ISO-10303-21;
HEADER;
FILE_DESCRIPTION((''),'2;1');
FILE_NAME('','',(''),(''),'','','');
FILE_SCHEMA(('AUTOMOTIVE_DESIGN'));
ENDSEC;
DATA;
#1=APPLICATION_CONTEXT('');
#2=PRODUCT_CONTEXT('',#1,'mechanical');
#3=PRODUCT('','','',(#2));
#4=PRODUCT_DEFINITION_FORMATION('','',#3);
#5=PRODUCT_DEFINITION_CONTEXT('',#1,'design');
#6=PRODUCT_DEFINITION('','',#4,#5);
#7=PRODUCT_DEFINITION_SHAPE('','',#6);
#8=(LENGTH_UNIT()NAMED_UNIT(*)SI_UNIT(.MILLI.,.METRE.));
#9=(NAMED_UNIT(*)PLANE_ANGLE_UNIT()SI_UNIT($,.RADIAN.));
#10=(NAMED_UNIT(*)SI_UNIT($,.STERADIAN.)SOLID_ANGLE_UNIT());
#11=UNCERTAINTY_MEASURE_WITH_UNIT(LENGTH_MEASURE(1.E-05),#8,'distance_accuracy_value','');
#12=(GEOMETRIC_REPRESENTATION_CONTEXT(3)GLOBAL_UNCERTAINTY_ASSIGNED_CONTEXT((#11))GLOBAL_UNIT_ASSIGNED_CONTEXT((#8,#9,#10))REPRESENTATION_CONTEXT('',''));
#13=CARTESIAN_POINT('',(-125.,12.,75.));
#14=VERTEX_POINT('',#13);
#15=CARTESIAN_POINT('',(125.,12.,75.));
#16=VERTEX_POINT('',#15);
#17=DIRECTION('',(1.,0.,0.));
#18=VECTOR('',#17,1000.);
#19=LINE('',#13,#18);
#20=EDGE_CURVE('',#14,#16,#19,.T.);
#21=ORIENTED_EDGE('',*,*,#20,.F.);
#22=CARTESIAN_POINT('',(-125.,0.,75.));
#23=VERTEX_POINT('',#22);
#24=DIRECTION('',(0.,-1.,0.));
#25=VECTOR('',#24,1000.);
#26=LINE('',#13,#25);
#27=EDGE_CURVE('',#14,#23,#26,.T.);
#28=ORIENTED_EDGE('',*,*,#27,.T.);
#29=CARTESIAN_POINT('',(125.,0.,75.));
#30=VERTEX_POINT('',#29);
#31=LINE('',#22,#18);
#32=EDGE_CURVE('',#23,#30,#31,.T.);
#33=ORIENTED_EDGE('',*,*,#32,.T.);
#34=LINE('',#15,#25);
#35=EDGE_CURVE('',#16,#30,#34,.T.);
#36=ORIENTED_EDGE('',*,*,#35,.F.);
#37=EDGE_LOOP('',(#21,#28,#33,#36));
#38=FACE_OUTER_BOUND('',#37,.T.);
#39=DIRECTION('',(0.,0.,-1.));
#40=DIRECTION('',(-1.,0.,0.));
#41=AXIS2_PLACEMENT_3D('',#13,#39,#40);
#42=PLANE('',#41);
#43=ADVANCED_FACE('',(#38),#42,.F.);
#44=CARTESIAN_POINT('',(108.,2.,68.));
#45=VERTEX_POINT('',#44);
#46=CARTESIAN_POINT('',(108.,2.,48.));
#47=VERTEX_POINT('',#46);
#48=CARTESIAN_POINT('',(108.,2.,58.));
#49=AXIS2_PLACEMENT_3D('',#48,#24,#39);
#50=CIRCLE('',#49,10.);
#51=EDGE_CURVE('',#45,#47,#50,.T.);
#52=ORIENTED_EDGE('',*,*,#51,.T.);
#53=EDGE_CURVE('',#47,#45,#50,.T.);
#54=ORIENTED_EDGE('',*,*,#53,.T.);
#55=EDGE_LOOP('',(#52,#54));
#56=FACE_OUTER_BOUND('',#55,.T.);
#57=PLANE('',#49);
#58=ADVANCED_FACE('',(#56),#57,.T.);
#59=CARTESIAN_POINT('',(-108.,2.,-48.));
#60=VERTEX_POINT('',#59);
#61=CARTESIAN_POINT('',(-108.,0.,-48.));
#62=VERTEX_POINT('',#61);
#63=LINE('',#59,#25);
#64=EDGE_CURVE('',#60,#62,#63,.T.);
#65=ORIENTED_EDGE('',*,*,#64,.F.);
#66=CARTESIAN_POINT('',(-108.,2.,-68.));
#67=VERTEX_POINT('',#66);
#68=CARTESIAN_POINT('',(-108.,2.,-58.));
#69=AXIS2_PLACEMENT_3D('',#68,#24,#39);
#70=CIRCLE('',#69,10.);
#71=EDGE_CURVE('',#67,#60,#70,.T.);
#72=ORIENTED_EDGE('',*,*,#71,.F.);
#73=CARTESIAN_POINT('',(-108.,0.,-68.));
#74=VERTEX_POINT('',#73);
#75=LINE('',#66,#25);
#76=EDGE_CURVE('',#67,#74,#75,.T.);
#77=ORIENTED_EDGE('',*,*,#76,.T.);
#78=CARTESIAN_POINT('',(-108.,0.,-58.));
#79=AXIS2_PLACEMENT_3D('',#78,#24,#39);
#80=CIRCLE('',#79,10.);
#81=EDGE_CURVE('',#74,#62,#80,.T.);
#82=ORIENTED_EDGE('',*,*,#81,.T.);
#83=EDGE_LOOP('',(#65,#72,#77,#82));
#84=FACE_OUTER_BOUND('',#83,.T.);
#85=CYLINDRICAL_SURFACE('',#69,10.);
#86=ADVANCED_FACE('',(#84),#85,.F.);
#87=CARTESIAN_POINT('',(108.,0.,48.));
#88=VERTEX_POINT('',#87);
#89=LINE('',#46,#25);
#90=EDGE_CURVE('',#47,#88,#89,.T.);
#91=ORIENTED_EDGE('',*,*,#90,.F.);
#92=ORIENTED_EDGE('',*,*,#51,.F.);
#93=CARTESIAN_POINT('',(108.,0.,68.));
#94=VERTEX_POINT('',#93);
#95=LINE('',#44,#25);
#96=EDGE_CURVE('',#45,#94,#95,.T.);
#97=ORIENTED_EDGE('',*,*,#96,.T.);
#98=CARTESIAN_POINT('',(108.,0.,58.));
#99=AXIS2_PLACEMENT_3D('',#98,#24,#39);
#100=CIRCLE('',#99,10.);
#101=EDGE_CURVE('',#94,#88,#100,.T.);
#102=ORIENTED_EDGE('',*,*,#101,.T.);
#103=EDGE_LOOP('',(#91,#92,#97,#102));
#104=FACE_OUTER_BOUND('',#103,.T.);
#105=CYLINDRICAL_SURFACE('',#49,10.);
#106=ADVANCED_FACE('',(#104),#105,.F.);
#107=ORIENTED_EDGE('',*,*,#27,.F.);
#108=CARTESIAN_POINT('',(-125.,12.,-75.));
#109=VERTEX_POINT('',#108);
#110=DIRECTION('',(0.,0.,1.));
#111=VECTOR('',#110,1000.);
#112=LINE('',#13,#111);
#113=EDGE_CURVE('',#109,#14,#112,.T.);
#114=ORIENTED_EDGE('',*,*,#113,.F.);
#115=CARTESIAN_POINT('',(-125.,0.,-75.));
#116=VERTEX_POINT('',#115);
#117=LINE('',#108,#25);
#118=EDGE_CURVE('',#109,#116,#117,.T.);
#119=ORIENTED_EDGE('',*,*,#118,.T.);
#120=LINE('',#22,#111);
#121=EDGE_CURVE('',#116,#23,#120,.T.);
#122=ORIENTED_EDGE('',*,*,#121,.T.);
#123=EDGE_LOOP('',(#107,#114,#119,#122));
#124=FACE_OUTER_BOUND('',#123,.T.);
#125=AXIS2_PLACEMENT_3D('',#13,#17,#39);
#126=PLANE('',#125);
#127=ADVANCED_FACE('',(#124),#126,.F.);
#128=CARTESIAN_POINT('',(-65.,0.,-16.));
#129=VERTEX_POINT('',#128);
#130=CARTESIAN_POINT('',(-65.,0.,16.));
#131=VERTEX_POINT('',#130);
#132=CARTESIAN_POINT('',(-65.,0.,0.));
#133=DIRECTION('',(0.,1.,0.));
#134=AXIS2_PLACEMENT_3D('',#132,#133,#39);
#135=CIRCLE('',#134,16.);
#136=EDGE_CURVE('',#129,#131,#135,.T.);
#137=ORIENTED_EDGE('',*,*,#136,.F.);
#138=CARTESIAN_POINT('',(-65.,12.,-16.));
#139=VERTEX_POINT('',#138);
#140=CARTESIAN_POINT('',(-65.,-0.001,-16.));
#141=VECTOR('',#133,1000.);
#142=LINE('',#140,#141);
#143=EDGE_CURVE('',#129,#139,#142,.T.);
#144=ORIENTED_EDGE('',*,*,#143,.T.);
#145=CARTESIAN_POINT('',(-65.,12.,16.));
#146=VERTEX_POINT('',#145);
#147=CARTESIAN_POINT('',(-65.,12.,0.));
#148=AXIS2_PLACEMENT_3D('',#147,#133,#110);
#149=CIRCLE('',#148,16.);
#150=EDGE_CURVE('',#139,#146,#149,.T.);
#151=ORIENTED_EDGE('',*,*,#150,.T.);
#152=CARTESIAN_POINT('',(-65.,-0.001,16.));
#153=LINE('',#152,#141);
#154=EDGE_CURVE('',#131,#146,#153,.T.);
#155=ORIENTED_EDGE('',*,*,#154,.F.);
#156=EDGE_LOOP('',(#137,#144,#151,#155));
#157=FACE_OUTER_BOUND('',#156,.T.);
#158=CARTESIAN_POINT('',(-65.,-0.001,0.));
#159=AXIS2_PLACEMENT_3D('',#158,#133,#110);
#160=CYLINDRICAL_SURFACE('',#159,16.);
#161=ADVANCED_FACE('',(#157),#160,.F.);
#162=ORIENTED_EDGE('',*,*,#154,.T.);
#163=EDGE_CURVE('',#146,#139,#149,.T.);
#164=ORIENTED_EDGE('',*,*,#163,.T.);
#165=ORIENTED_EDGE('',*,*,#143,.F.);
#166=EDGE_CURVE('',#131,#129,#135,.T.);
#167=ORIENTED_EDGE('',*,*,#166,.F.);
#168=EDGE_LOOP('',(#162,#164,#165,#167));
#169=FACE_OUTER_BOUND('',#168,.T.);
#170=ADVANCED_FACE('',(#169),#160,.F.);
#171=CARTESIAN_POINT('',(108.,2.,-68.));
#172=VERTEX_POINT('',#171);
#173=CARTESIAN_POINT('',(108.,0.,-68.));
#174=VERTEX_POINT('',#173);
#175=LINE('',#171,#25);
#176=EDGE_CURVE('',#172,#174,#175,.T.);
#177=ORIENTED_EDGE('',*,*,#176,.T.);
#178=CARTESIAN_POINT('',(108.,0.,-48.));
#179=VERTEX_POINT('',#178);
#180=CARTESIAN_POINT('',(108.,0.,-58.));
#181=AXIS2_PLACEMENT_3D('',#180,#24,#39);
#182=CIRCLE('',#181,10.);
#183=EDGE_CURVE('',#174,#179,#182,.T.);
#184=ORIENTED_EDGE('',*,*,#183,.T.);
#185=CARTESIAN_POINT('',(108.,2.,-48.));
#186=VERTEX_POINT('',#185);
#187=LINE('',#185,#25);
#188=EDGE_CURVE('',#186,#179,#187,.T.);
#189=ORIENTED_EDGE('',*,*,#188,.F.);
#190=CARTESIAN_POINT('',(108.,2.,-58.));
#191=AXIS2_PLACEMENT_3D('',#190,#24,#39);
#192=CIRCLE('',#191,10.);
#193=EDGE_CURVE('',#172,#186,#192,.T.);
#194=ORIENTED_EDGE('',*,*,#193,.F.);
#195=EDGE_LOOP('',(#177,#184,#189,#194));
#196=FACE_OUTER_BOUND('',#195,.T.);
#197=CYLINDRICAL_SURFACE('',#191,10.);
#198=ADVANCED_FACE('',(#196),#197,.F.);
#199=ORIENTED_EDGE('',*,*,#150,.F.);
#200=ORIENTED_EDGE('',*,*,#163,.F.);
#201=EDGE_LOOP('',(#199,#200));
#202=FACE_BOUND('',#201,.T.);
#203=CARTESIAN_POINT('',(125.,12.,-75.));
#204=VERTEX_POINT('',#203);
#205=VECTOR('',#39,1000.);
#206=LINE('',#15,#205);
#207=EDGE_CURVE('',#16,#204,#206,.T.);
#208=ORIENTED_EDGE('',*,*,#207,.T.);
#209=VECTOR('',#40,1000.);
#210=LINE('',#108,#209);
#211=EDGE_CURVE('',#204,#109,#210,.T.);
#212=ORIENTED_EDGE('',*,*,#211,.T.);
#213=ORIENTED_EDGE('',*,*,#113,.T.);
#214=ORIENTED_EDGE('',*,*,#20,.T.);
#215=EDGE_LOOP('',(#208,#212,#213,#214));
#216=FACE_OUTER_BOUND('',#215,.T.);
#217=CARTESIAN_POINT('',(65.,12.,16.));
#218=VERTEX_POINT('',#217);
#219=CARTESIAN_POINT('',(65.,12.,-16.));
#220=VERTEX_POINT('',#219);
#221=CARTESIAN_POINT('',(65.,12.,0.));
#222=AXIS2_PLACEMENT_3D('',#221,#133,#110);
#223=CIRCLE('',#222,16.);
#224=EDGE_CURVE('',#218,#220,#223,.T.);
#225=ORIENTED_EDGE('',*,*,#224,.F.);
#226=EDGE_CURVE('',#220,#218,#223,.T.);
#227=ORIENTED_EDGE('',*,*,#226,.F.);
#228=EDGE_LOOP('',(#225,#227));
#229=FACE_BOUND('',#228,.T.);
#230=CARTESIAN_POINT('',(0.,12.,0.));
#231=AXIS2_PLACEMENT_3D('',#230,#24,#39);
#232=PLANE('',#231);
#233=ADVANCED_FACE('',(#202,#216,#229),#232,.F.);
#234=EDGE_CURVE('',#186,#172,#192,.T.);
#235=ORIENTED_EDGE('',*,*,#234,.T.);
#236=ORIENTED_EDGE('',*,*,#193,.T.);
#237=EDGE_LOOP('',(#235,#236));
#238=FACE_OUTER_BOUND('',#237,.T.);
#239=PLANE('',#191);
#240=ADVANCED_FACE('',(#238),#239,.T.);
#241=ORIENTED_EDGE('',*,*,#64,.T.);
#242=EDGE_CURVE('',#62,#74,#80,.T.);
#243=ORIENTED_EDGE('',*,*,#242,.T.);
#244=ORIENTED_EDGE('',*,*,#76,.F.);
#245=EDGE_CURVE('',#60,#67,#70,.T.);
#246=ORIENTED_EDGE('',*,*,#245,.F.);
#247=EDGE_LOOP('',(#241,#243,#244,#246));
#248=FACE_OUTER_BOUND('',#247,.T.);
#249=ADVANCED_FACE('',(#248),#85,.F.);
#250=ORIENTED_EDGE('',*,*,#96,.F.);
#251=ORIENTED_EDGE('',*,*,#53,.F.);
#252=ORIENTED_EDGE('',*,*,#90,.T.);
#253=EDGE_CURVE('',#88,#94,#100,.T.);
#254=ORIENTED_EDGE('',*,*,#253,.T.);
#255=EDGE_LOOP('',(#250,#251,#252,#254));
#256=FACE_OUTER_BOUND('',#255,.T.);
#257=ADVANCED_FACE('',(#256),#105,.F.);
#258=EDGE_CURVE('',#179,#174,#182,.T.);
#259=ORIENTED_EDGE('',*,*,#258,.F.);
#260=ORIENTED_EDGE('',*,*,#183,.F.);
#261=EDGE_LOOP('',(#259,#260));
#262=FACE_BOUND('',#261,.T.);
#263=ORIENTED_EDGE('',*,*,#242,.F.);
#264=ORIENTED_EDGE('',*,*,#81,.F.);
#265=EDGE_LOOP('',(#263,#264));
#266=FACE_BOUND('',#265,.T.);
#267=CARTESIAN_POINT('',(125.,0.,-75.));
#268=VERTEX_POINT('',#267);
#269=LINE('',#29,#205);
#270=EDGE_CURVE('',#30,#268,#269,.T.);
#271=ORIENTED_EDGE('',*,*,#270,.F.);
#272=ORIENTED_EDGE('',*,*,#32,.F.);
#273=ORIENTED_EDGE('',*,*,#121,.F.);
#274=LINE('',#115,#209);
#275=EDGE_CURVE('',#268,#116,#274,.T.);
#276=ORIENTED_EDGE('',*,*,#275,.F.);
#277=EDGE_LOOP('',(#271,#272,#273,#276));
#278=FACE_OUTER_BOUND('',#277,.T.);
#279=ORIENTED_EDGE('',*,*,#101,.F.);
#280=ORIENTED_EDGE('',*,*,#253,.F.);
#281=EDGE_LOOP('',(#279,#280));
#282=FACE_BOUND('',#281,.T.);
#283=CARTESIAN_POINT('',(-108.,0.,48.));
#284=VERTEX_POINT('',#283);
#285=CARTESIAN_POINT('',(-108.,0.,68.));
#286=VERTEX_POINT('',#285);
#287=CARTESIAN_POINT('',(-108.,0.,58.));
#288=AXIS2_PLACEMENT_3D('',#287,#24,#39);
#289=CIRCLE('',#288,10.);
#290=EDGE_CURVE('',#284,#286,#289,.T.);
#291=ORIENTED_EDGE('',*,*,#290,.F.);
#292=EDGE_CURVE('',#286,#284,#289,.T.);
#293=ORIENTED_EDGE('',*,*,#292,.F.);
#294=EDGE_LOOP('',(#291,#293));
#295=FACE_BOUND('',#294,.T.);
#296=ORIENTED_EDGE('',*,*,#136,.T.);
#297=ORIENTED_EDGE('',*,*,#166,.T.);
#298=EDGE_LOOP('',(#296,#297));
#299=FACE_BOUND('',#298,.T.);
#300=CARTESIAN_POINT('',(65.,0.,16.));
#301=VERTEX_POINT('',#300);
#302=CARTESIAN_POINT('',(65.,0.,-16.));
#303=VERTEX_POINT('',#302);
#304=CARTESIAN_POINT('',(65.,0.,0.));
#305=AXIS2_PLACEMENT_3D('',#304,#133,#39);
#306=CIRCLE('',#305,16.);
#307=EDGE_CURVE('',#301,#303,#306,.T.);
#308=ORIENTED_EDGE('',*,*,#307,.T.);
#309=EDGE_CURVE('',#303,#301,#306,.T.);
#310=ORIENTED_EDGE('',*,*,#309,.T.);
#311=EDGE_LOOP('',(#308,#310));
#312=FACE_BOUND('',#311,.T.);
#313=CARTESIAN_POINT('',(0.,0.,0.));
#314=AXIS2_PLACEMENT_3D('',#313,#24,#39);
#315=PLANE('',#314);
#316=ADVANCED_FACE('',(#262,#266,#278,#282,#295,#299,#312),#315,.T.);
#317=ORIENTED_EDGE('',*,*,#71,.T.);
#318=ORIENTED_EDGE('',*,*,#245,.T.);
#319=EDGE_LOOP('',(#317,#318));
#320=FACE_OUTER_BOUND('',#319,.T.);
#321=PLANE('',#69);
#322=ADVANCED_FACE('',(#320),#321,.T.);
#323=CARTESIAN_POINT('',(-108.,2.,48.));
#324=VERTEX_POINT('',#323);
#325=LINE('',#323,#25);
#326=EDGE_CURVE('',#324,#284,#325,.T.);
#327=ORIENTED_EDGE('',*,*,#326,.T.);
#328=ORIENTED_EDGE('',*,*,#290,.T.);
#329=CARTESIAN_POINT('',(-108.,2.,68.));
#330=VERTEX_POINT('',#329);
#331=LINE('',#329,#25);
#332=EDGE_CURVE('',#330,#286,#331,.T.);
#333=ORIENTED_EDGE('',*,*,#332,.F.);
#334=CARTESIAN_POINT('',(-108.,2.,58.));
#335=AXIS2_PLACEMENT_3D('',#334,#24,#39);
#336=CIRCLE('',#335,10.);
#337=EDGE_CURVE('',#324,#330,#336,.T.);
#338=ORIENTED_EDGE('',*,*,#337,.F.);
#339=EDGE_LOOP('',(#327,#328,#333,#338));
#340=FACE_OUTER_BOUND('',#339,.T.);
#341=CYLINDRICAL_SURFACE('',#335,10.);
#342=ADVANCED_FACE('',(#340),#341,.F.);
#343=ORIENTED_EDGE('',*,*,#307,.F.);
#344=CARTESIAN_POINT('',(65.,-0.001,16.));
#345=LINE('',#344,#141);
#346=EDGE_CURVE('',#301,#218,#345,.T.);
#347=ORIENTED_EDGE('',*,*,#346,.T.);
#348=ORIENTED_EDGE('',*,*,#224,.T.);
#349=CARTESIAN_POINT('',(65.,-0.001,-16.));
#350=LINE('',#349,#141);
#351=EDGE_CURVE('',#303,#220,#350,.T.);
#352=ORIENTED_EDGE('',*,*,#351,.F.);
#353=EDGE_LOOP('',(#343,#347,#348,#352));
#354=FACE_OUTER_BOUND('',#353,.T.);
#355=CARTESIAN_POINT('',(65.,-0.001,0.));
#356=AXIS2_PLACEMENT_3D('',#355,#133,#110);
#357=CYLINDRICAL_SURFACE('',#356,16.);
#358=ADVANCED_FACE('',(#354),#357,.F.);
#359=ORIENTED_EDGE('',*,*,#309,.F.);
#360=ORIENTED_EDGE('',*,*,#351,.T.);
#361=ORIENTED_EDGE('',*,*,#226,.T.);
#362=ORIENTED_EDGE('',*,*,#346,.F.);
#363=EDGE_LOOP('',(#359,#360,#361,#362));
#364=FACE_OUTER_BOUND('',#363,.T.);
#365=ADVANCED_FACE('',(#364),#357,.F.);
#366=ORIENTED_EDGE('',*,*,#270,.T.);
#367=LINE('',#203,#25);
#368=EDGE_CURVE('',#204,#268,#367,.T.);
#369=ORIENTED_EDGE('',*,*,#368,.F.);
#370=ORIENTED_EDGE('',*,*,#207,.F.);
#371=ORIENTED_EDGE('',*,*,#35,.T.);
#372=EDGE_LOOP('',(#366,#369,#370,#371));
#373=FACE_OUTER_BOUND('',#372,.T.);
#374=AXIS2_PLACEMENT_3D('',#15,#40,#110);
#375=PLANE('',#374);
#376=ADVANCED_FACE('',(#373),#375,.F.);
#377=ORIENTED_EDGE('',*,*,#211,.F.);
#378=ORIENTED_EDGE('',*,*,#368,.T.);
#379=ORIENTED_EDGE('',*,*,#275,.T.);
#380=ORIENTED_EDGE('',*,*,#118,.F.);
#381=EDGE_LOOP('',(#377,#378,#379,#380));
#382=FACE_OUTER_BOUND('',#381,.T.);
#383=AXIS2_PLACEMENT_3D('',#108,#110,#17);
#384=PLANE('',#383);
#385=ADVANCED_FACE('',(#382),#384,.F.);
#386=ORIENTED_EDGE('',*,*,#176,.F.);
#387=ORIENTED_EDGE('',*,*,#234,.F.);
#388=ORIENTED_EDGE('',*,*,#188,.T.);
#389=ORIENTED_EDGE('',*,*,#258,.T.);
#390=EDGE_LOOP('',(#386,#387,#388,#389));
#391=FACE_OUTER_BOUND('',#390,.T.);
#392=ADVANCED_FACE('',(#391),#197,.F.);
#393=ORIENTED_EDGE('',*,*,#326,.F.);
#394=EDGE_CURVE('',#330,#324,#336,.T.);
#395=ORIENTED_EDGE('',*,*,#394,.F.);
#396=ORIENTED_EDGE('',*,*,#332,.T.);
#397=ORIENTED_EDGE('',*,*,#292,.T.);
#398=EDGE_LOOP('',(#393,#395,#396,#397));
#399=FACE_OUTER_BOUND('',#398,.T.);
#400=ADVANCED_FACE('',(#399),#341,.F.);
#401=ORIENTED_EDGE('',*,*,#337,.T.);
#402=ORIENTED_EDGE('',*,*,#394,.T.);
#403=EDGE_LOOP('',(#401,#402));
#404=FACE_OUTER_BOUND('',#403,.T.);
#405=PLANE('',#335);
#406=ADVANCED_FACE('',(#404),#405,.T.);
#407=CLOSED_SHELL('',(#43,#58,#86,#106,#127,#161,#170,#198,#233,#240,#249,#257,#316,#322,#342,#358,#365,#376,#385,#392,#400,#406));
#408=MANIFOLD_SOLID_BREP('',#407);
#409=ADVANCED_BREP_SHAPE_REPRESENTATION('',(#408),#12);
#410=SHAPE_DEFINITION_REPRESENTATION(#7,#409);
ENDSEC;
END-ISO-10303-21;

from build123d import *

# Parameters (mm, degrees)
SKETCH_1_W          = 250
SKETCH_1_H          = 150
EXTRUDE_1_DEPTH     = 12
SKETCH_2_R          = 10
CUT_EXTRUDE_1_DEPTH = 2
CUT_EXTRUDE_2_REACH = 148.267
SKETCH_3_R          = 16


with BuildPart() as part:
    # 草图1 → 凸台-拉伸1 (new body)
    with BuildSketch(Plane(origin=(0, 0, 0), x_dir=(1, 0, 0), z_dir=(0, 1, 0))):
        Rectangle(SKETCH_1_W, SKETCH_1_H)
    extrude(amount=EXTRUDE_1_DEPTH)

    # 草图2 → 切除-拉伸1 (cut)
    with BuildSketch(Plane(origin=(0, 0, 0), x_dir=(-1, 0, 0), z_dir=(0, -1, 0))):
        with Locations(Location((-108, 58, 0), (0, 0, 90))):
            Circle(SKETCH_2_R)
        with Locations(Location((108, 58, 0), (0, 0, 90))):
            Circle(SKETCH_2_R)
        with Locations(Location((-108, -58, 0), (0, 0, 90))):
            Circle(SKETCH_2_R)
        with Locations(Location((108, -58, 0), (0, 0, 90))):
            Circle(SKETCH_2_R)
    extrude(amount=-CUT_EXTRUDE_1_DEPTH, mode=Mode.SUBTRACT)

    # 草图3 → 切除-拉伸2 (cut, up to next)
    with BuildSketch(Plane(origin=(0, 12, 0), x_dir=(1, 0, 0), z_dir=(0, 1, 0)), mode=Mode.PRIVATE) as cut_extrude_2_sk1:
        with Locations(Location((-65, 0, 0), (0, 0, 270))):
            Circle(SKETCH_3_R)
    cut_extrude_2_tool1 = extrude(cut_extrude_2_sk1.sketch, amount=-CUT_EXTRUDE_2_REACH, mode=Mode.PRIVATE) & part.part
    # 草图3 → 切除-拉伸2 (cut, up to next)
    with BuildSketch(Plane(origin=(0, 12, 0), x_dir=(1, 0, 0), z_dir=(0, 1, 0)), mode=Mode.PRIVATE) as cut_extrude_2_sk2:
        with Locations(Location((65, 0, 0), (0, 0, 270))):
            Circle(SKETCH_3_R)
    cut_extrude_2_tool2 = extrude(cut_extrude_2_sk2.sketch, amount=-CUT_EXTRUDE_2_REACH, mode=Mode.PRIVATE) & part.part
    add(cut_extrude_2_tool1.solids().sort_by_distance((-65, 12, 0))[0], mode=Mode.SUBTRACT)
    add(cut_extrude_2_tool2.solids().sort_by_distance((65, 12, 0))[0], mode=Mode.SUBTRACT)


solid = part.part
